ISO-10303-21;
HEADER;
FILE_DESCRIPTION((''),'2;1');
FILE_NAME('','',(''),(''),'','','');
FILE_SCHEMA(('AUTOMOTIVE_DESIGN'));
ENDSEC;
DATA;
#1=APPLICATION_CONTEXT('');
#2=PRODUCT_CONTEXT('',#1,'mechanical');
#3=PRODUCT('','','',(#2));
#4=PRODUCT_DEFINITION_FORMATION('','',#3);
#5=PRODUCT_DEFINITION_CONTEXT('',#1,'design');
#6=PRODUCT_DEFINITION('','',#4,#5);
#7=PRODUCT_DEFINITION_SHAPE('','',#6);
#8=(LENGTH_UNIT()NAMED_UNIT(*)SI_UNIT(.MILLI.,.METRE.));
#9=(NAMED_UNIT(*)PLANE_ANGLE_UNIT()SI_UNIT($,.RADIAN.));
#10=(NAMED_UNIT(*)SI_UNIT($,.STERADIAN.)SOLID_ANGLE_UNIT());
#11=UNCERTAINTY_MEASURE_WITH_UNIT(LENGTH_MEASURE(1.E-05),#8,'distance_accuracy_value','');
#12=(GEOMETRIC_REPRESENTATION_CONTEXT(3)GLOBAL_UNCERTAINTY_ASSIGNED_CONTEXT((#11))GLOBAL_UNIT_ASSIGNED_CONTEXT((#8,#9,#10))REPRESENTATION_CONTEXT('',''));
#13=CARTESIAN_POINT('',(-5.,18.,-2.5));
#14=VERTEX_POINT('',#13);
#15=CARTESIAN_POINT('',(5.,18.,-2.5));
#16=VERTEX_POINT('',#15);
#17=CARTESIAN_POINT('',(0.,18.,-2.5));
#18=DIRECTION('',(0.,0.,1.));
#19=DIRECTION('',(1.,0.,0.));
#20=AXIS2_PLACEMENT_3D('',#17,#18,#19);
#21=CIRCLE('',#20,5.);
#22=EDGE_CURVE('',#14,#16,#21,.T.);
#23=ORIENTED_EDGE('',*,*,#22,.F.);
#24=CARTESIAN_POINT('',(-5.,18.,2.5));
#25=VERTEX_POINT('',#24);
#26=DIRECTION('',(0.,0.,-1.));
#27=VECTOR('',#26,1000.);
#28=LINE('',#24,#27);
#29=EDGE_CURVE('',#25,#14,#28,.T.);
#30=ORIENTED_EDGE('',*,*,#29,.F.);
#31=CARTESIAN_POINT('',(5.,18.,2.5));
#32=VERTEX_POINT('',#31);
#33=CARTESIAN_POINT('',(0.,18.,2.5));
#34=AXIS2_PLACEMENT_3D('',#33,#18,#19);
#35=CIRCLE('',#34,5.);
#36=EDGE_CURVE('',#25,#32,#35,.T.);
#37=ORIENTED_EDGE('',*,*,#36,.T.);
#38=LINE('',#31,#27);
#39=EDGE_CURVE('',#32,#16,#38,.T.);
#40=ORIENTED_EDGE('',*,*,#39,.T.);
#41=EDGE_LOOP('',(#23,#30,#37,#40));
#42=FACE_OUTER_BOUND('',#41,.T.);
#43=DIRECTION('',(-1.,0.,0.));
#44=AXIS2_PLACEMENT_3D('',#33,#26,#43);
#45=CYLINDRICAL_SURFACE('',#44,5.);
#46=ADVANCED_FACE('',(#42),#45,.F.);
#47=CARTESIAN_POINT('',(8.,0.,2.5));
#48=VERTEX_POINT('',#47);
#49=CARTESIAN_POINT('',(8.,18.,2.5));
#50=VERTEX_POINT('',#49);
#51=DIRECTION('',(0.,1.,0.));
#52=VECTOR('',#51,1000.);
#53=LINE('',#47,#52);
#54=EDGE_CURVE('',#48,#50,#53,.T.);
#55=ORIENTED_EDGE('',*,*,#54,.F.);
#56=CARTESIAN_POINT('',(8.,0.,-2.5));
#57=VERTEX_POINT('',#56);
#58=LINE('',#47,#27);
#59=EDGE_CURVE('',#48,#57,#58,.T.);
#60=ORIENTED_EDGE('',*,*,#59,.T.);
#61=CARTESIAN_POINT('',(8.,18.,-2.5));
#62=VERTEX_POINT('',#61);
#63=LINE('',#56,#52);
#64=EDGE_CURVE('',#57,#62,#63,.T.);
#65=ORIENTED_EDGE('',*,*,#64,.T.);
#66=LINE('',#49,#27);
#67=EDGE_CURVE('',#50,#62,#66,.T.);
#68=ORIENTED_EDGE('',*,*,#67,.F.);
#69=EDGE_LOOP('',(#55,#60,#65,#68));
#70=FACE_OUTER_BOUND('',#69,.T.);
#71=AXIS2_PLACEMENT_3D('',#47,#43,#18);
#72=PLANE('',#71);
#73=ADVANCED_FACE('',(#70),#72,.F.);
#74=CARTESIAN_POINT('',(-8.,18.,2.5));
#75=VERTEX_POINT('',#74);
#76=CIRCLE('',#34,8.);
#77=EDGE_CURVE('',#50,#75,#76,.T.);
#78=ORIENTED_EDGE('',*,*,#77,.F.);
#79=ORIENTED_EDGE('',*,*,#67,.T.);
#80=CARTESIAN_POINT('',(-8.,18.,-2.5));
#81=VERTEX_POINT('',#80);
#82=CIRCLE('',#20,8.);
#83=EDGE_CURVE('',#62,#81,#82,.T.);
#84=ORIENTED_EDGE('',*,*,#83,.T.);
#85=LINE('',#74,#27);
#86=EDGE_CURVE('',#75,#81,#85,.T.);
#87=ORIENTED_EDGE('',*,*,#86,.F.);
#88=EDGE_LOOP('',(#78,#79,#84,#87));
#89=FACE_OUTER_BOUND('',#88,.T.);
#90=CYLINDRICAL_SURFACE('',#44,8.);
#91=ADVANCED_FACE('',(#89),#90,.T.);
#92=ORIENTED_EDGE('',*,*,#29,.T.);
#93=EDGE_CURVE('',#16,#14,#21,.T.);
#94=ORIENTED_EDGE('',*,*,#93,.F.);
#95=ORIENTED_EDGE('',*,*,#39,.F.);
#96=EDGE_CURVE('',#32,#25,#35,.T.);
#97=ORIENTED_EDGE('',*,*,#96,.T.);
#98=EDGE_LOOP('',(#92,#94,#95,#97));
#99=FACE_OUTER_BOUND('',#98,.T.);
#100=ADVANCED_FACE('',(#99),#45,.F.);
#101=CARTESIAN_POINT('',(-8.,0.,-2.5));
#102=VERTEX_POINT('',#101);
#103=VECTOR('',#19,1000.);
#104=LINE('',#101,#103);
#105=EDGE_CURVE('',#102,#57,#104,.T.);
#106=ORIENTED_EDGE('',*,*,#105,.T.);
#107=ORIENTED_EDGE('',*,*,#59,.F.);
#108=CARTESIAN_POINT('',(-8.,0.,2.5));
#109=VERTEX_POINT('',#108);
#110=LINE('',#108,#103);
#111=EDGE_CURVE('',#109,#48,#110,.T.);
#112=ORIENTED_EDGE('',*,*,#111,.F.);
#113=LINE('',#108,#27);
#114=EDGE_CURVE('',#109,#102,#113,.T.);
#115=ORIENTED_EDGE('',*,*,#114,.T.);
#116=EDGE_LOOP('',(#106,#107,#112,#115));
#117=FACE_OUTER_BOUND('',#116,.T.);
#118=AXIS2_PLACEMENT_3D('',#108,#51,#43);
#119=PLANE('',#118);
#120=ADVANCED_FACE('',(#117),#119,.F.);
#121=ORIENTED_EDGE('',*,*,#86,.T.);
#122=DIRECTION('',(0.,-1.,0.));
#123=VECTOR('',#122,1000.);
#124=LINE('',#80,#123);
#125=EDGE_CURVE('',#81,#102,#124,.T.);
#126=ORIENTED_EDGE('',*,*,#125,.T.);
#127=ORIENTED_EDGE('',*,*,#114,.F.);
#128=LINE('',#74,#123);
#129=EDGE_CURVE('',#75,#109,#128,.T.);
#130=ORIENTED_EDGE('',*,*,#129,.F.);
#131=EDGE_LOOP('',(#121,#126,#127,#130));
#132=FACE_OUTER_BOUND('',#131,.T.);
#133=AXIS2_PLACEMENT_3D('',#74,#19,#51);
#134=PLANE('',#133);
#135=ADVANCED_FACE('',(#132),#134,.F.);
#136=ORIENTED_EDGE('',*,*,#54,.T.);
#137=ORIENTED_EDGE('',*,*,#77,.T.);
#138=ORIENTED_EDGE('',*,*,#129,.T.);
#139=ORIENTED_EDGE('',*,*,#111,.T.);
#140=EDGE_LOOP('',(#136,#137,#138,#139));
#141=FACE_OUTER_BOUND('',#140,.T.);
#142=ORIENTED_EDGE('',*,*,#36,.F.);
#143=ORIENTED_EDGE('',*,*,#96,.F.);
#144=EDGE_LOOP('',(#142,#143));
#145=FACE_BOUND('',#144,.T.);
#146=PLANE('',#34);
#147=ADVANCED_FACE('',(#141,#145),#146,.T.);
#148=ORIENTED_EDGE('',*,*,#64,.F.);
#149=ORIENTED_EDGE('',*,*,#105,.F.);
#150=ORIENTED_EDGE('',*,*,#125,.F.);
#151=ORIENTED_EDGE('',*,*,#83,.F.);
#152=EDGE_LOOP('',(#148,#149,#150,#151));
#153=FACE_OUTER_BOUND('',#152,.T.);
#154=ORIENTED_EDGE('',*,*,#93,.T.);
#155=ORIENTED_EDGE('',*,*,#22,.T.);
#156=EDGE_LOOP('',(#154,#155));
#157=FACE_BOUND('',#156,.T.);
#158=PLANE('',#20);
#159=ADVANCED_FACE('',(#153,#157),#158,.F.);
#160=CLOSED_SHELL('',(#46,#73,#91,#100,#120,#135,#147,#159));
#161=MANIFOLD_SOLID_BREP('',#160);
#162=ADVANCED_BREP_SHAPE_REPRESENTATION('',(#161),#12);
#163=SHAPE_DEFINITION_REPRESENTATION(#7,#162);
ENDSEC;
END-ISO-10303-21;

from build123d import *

# Parameters (mm, degrees)
SKETCH_1_R      = 5
EXTRUDE_1_DEPTH = 2.5


with BuildPart() as part:
    # 草图1 → 凸台-拉伸1 (new, symmetric)
    with BuildSketch(Plane.XY):
        with BuildLine():
            Line((8, 0), (8, 18))
            ThreePointArc((8, 18), (0, 26), (-8, 18))
            Line((-8, 18), (-8, 0))
            Line((-8, 0), (8, 0))
        make_face()
        with Locations((0, 18)):
            Circle(SKETCH_1_R, mode=Mode.SUBTRACT)
    extrude(amount=EXTRUDE_1_DEPTH, both=True)


solid = part.part
